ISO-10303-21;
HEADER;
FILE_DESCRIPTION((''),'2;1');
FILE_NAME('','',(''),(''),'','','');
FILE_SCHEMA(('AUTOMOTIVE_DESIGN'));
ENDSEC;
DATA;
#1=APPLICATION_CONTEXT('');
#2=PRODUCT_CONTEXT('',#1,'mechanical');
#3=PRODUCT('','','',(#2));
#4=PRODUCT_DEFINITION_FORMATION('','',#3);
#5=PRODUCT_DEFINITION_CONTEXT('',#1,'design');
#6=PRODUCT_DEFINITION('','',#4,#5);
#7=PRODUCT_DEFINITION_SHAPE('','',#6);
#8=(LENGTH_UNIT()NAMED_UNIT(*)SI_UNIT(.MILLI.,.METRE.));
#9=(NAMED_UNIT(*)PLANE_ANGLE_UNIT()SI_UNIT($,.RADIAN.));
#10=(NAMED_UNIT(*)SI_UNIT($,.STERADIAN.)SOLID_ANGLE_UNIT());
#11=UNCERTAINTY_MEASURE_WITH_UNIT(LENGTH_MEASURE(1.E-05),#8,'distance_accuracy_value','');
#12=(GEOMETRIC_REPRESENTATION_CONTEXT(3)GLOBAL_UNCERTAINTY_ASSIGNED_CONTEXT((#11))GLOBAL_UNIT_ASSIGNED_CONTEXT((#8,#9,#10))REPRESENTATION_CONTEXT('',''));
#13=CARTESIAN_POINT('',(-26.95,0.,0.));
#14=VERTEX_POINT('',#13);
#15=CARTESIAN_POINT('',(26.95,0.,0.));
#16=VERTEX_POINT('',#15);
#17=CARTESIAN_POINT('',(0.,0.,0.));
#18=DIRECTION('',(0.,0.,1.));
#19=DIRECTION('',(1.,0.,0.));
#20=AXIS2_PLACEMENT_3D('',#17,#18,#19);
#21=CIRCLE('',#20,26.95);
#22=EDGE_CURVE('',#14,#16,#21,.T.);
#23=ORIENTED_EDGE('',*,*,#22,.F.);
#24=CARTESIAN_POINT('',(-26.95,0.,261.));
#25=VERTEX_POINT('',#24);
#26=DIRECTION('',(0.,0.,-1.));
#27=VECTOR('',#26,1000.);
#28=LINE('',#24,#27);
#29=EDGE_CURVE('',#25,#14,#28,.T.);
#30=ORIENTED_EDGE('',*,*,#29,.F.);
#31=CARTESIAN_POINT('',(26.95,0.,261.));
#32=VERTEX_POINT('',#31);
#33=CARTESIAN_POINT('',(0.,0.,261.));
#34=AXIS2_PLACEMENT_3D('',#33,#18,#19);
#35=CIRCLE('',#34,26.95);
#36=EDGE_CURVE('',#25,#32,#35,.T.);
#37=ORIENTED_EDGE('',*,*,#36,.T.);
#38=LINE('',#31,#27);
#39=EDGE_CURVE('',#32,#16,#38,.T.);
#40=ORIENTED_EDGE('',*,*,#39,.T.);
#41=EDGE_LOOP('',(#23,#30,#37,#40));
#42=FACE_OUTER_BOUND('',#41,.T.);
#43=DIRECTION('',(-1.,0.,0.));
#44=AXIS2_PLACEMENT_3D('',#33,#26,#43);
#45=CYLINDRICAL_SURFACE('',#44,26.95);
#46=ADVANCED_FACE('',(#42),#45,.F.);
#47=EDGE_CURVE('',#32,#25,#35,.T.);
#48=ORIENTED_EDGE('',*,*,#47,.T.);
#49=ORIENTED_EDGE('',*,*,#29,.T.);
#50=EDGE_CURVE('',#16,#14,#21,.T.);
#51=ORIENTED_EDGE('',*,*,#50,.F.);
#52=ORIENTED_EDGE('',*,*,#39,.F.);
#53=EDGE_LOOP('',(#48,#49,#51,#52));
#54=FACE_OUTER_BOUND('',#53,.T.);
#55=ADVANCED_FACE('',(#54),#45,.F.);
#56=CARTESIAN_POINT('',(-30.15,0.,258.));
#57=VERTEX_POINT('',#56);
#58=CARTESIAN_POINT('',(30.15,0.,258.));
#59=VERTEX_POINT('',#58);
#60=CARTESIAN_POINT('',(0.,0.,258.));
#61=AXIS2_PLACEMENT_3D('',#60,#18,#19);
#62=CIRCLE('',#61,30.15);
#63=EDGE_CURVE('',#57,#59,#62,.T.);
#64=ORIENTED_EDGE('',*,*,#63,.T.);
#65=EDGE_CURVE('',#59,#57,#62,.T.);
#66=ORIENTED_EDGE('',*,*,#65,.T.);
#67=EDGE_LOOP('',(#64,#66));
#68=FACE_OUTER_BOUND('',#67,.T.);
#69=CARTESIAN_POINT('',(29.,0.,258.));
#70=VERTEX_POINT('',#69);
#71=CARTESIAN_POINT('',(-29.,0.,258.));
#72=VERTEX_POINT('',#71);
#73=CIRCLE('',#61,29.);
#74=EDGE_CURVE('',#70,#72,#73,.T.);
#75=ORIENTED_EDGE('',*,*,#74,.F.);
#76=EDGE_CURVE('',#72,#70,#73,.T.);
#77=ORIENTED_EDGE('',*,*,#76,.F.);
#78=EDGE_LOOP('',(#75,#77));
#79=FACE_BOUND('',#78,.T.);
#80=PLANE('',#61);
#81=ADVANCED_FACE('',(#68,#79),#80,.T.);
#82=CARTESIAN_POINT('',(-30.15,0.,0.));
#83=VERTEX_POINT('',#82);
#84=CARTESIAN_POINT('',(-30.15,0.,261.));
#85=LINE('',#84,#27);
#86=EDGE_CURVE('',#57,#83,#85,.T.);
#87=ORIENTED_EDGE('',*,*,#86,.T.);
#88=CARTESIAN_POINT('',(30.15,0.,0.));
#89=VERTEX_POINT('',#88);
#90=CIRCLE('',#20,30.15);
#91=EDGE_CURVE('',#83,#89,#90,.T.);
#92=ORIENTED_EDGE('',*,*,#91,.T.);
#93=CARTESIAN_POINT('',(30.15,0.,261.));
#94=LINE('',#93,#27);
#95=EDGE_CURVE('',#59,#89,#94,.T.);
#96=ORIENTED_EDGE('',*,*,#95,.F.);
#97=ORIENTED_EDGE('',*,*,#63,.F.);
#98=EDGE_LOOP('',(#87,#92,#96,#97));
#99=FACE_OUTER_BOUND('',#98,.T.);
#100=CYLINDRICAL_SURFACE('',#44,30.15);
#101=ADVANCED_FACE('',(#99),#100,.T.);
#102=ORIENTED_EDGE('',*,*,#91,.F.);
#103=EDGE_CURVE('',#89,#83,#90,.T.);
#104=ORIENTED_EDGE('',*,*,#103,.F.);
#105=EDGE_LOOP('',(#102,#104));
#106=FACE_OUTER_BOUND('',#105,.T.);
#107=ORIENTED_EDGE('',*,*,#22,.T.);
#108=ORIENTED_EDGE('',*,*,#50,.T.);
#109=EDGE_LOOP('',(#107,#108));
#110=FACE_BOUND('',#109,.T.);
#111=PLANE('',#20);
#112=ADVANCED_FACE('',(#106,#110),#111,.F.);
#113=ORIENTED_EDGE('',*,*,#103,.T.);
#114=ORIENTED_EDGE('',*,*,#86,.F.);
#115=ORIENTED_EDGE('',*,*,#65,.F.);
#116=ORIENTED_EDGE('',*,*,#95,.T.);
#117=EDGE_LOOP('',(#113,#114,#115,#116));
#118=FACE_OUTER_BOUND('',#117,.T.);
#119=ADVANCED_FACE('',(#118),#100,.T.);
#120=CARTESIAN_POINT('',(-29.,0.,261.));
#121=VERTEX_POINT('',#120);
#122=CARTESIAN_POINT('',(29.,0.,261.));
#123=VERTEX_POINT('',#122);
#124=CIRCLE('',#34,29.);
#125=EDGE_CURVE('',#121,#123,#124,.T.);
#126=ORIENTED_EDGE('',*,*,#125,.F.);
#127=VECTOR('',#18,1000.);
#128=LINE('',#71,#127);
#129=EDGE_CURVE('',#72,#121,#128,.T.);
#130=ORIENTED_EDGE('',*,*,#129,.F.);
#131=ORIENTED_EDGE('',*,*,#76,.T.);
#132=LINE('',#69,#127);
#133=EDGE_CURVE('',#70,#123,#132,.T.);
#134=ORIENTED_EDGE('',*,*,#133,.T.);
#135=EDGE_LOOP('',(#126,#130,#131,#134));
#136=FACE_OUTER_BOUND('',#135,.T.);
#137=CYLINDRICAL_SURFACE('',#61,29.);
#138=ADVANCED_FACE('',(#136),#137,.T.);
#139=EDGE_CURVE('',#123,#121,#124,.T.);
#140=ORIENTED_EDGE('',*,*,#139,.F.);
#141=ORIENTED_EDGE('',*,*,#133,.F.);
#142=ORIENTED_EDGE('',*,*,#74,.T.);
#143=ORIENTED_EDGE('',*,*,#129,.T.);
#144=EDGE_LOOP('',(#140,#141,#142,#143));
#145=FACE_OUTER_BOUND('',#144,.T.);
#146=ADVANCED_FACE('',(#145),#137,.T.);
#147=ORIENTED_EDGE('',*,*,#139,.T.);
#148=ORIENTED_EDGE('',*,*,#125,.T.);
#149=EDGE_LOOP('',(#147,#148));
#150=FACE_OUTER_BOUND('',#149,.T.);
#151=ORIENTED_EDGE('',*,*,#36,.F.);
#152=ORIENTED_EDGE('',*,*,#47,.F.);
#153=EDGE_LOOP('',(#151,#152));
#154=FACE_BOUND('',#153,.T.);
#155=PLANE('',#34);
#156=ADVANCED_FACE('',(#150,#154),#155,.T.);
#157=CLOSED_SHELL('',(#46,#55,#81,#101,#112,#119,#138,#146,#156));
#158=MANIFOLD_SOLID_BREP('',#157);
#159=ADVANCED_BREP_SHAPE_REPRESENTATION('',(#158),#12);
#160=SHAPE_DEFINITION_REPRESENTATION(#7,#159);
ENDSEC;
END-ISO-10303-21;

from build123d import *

# Parameters (mm, degrees)
SKETCH_1_R          = 30.15
EXTRUDE_1_DEPTH     = 261
SHELL_1_T           = -3.2
SKETCH_2_OUTSIDE_W  = 117.216
SKETCH_2_OUTSIDE_H  = 117.216
SKETCH_2_OUTSIDE_R  = 29
CUT_EXTRUDE_1_DEPTH = 3


with BuildPart() as part:
    # 草图1 → 凸台-拉伸1 (new body)
    with BuildSketch(Plane.XY):
        Circle(SKETCH_1_R)
    extrude(amount=EXTRUDE_1_DEPTH)

    # 抽壳1
    shell_1_openings = [part.faces().sort_by_distance(p)[0] for p in [
        (0, 0, 261),
        (0, 0, 0),
    ]]
    offset(amount=SHELL_1_T, openings=shell_1_openings, kind=Kind.INTERSECTION)

    # 草图2 outside → 切除-拉伸1 (cut)
    with BuildSketch(Plane.XY.offset(261)):
        Rectangle(SKETCH_2_OUTSIDE_W, SKETCH_2_OUTSIDE_H)
        Circle(SKETCH_2_OUTSIDE_R, mode=Mode.SUBTRACT)
    extrude(amount=-CUT_EXTRUDE_1_DEPTH, mode=Mode.SUBTRACT)


solid = part.part
